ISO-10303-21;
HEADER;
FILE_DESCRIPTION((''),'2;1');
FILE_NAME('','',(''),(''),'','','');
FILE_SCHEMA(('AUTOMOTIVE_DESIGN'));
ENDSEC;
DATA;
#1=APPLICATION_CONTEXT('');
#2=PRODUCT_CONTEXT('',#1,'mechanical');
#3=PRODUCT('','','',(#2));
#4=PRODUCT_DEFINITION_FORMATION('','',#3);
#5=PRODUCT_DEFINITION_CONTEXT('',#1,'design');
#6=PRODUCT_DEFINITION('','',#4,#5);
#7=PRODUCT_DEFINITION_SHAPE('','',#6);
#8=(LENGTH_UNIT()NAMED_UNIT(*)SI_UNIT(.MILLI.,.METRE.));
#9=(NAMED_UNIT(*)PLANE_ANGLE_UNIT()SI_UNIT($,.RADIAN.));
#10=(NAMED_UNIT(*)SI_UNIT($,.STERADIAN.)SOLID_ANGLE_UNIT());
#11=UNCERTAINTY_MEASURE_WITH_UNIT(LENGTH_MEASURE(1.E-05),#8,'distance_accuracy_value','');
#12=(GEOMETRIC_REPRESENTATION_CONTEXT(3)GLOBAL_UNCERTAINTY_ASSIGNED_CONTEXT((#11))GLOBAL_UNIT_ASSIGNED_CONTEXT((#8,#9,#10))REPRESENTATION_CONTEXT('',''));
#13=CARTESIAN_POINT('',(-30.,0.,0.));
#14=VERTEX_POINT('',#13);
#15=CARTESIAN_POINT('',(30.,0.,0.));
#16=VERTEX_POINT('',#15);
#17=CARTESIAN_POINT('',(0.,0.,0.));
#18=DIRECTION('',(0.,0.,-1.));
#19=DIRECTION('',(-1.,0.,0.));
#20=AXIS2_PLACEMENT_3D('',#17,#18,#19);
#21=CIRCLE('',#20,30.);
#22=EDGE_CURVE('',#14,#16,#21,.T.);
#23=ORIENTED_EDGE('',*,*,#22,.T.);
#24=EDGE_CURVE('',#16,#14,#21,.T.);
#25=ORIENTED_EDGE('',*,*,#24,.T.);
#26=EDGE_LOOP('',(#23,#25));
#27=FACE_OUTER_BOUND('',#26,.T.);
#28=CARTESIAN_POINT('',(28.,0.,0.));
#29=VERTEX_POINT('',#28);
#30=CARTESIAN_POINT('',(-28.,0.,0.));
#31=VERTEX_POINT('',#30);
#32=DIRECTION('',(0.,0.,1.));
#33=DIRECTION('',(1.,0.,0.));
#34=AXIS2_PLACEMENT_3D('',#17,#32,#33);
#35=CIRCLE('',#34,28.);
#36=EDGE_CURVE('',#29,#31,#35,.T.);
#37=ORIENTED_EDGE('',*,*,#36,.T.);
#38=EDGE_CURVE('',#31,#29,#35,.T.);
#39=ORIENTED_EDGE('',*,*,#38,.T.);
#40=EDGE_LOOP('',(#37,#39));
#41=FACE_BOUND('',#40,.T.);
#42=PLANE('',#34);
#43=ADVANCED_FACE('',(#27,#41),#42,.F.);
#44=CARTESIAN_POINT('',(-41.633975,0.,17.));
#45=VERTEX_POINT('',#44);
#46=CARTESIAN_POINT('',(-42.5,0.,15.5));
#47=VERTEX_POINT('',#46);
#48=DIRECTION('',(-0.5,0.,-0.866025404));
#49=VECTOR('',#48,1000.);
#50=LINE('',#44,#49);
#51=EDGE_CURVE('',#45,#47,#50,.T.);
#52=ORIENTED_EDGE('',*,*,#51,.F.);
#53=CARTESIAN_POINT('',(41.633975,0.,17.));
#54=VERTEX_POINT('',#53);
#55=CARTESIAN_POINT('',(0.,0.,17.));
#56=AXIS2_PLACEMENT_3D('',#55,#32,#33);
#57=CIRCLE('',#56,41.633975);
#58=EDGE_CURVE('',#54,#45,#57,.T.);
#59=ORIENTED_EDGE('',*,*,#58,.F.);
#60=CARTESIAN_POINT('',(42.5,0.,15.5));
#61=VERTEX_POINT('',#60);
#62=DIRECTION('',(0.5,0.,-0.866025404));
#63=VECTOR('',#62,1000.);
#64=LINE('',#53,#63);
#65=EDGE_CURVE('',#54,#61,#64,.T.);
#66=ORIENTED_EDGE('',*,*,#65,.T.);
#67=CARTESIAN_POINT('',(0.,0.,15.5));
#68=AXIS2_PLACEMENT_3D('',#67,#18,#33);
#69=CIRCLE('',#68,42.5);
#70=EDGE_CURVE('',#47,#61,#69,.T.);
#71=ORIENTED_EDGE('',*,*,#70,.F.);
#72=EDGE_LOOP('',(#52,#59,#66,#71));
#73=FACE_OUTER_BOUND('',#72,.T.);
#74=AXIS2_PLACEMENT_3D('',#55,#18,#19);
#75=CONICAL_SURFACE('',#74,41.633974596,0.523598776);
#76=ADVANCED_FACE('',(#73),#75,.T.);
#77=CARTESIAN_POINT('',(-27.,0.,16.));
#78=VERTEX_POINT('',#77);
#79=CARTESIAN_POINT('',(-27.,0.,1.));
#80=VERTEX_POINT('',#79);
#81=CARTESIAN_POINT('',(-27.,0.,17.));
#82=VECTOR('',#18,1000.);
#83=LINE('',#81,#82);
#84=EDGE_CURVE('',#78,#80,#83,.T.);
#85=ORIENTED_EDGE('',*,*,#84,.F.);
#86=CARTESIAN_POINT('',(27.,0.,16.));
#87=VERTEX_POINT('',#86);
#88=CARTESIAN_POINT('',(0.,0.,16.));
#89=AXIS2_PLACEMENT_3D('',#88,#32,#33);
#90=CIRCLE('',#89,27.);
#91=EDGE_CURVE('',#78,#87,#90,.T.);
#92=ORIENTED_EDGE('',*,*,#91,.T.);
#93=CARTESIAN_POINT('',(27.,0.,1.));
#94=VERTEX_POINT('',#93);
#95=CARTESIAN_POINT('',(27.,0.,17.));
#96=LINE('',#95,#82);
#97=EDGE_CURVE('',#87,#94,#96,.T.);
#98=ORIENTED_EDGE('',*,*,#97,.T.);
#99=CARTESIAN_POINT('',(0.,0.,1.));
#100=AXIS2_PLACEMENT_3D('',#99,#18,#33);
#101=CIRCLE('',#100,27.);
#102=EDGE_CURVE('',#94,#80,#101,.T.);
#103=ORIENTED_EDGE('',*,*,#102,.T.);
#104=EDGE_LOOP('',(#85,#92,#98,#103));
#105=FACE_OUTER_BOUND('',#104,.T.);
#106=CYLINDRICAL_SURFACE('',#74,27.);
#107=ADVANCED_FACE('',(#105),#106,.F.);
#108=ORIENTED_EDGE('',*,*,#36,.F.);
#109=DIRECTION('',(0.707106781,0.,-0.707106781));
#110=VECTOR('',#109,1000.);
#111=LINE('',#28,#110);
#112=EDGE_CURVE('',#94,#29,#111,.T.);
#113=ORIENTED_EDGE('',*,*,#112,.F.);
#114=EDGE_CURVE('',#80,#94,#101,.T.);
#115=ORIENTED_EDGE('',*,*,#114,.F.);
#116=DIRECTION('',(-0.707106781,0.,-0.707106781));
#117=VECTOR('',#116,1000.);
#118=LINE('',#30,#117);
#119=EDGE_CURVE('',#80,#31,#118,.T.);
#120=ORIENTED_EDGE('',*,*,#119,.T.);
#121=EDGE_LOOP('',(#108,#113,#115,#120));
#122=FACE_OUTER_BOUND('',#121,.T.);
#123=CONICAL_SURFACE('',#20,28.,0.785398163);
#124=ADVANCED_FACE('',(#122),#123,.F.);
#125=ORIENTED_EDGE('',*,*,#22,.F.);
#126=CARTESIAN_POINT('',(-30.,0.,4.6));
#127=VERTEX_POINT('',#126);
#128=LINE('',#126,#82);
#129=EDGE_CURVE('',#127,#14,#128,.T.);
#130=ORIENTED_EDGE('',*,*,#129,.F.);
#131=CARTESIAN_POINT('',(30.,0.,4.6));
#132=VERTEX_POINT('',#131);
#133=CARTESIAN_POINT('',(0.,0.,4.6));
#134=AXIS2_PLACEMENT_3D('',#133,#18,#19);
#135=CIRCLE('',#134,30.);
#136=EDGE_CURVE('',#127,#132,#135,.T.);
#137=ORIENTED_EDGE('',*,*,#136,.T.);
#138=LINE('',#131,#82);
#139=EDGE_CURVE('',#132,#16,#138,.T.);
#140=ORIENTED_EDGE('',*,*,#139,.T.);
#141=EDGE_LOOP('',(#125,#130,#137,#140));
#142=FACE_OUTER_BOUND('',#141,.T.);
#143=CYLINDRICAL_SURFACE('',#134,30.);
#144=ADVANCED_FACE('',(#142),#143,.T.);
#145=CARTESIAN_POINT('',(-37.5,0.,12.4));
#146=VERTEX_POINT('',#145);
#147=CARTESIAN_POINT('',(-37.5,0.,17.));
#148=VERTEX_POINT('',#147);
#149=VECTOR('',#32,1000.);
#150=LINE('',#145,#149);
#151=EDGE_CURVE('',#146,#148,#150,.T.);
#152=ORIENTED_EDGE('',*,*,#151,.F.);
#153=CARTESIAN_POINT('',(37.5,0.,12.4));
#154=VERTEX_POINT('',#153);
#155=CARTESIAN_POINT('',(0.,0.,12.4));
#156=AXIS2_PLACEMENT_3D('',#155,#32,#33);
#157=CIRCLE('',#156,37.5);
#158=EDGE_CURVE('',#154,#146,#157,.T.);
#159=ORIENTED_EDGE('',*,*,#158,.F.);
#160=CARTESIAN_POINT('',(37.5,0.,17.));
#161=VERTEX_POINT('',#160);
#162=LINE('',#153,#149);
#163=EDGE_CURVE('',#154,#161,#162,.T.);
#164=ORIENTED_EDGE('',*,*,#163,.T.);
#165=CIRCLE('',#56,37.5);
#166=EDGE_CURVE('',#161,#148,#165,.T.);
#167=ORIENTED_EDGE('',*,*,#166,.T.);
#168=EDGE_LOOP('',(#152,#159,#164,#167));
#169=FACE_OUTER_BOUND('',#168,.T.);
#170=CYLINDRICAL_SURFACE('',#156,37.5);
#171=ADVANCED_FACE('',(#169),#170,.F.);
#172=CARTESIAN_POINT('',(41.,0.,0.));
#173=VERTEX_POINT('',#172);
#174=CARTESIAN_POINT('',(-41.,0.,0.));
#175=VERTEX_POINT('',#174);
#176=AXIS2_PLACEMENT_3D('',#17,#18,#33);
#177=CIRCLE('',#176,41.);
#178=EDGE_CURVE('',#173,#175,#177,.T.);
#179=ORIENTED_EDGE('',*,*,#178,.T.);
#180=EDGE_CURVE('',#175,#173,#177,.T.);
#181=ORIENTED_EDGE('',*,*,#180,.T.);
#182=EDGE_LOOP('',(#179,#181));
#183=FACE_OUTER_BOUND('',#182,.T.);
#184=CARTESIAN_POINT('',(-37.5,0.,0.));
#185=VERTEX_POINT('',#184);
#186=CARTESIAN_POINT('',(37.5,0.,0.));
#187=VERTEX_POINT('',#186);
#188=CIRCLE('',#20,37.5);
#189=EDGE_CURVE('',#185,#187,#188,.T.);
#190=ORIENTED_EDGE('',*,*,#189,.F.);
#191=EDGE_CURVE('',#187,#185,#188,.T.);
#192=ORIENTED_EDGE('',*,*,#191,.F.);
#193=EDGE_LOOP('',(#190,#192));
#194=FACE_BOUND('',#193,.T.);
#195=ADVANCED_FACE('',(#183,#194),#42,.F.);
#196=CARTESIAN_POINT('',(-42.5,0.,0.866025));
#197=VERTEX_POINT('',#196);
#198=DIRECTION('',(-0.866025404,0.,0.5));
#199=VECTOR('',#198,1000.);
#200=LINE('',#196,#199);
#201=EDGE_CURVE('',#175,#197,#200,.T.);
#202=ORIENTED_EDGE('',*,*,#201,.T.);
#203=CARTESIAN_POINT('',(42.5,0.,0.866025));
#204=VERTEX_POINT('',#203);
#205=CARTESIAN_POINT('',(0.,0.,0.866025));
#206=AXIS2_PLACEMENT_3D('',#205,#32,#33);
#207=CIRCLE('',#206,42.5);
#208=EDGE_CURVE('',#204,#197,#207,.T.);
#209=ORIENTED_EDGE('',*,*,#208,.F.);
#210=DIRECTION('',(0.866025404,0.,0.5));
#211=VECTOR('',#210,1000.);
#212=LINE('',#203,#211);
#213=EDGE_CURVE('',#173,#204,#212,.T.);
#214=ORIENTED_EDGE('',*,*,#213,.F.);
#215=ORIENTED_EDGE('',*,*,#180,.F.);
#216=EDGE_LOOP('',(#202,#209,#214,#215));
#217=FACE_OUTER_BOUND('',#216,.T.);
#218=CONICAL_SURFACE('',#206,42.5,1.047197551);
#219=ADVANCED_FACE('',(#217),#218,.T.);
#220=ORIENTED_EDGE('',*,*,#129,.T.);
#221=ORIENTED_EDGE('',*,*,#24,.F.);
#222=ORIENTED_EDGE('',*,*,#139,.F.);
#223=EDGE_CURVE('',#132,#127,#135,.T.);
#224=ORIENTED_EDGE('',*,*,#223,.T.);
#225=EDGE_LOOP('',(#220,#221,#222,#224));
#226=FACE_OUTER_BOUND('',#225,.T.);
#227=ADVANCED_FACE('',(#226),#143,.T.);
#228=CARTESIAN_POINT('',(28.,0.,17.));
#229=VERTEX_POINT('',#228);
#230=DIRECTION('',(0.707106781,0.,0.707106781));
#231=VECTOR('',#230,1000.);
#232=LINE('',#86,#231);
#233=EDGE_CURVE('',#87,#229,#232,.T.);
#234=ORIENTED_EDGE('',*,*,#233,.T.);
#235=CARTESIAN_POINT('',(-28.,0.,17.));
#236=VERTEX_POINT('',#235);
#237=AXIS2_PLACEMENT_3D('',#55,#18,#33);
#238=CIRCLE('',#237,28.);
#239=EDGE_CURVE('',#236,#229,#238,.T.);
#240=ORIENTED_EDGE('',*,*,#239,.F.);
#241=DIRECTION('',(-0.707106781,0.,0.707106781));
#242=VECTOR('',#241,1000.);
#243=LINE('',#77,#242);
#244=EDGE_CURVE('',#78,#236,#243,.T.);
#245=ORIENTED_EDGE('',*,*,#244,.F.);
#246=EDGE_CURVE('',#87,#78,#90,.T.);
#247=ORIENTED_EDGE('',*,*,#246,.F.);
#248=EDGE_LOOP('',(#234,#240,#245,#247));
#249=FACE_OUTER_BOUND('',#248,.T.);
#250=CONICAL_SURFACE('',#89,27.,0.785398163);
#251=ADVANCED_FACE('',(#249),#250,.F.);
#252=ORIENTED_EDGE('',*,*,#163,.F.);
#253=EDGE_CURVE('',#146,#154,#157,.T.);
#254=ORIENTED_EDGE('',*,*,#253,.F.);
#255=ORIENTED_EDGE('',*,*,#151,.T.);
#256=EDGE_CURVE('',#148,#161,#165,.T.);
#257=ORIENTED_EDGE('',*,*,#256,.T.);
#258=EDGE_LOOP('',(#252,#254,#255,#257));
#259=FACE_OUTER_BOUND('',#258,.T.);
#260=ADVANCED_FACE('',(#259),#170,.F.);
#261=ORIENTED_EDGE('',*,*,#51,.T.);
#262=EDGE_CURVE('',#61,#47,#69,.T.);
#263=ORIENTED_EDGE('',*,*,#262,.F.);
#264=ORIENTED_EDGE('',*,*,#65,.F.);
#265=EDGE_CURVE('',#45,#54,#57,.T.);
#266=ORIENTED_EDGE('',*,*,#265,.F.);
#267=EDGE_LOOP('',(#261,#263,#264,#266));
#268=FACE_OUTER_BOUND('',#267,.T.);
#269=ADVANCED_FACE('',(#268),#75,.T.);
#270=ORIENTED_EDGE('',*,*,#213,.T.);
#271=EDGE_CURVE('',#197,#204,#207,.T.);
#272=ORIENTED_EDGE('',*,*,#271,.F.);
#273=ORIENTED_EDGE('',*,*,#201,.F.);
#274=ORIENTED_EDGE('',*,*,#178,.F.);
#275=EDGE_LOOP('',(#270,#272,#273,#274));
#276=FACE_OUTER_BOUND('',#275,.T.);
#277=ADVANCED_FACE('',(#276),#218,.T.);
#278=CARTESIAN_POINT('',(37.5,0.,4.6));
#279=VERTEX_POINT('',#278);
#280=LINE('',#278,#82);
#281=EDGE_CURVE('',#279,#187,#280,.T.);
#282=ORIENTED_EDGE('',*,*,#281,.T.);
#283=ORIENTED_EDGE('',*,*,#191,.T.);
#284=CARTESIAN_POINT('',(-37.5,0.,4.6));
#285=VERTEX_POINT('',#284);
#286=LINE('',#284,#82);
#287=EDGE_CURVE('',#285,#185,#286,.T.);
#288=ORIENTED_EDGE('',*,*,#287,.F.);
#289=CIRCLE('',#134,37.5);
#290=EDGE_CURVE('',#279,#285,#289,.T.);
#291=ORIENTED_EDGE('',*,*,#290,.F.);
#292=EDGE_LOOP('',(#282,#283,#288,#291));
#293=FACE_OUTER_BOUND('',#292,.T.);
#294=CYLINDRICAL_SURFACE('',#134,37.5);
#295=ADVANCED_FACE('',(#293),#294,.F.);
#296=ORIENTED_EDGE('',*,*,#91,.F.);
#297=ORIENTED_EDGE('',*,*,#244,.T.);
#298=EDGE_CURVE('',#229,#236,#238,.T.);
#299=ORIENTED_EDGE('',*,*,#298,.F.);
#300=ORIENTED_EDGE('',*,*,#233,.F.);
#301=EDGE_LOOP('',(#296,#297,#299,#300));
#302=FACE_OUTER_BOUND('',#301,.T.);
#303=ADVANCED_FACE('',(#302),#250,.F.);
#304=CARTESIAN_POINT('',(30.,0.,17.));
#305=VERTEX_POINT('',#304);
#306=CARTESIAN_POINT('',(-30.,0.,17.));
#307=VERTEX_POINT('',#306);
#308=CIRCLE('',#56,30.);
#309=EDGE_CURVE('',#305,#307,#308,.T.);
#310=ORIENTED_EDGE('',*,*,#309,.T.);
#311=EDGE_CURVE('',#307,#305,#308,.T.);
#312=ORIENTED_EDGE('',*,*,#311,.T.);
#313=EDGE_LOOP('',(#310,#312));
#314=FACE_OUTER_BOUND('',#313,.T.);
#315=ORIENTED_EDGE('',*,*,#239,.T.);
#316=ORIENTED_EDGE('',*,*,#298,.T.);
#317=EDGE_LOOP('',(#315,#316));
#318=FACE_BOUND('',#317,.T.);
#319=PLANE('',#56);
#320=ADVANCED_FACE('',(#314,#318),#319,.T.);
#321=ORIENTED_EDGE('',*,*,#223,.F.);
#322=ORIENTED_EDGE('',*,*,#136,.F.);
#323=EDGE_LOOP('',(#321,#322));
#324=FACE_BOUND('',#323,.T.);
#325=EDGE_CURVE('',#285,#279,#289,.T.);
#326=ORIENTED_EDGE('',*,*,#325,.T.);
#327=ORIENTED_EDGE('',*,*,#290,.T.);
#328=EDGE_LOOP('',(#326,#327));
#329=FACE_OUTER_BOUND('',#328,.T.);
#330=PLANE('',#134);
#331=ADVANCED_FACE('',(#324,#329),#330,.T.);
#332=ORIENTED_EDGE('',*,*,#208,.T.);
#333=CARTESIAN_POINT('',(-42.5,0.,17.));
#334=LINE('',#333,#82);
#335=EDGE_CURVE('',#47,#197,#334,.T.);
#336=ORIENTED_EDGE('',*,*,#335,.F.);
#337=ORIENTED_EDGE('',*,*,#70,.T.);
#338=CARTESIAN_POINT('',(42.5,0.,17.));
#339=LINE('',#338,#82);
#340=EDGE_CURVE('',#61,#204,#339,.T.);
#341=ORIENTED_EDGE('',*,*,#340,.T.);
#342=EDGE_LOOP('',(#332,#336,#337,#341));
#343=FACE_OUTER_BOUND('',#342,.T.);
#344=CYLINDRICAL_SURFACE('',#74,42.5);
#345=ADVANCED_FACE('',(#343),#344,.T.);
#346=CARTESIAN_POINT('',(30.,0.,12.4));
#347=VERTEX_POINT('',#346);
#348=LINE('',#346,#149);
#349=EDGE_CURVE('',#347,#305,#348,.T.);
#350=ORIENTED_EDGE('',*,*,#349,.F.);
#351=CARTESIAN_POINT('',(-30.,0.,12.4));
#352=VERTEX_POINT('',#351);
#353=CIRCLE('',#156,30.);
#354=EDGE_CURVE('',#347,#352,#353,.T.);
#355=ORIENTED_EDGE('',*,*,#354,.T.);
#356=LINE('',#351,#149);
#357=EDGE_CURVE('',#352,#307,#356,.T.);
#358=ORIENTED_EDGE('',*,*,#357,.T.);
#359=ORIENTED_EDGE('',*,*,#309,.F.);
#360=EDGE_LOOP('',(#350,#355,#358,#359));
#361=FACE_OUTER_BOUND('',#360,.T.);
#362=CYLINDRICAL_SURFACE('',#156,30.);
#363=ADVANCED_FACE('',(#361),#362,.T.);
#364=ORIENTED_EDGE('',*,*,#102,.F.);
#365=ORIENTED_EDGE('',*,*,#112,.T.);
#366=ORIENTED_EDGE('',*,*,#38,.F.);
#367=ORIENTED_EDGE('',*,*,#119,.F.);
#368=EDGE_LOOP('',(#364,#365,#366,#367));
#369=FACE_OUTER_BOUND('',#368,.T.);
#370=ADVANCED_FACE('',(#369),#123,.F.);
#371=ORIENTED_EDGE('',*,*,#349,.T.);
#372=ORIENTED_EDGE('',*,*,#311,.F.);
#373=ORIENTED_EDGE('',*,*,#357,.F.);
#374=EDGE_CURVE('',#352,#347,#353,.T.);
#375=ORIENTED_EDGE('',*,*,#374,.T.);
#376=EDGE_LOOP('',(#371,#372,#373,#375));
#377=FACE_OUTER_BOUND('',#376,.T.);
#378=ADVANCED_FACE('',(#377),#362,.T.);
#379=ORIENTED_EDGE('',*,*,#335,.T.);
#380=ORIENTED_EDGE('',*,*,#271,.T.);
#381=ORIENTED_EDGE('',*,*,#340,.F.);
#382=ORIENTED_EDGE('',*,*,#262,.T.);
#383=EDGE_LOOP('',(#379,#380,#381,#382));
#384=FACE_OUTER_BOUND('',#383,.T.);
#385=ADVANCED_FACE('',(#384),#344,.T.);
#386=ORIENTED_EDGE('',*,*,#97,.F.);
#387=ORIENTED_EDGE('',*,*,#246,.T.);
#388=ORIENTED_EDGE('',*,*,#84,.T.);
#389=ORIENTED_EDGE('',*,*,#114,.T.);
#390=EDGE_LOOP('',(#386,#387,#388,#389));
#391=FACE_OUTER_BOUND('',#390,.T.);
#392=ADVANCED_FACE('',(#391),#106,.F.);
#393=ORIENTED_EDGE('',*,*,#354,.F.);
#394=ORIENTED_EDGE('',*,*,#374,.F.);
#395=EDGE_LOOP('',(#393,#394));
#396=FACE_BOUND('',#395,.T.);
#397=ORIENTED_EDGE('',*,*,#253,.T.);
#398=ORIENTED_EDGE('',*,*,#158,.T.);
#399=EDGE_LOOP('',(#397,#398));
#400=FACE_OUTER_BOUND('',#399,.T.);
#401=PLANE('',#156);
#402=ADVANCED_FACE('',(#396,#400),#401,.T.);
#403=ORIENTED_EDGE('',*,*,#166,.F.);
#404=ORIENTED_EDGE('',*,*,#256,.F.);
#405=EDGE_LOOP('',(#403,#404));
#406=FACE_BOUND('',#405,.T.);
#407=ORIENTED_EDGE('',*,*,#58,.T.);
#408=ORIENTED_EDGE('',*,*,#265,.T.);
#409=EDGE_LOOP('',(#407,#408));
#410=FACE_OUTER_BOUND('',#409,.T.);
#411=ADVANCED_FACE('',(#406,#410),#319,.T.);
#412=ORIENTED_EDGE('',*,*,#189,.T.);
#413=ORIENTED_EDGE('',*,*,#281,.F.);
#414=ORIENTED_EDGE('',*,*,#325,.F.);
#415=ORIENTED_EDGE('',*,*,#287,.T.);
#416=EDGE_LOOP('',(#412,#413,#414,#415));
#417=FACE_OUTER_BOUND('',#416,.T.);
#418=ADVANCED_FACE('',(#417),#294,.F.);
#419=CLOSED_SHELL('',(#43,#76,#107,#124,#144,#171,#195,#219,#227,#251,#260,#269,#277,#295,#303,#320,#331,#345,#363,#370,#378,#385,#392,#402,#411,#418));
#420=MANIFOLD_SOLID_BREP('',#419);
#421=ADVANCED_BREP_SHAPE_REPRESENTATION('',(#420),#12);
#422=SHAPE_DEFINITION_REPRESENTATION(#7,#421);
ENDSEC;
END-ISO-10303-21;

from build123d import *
from OCP.BRepFilletAPI import BRepFilletAPI_MakeChamfer

# Parameters (mm, degrees)
SKETCH1_R           = 42.5
SKETCH1_R_2         = 27
BOSS_EXTRUDE1_DEPTH = 17
SKETCH2_R           = 37.5
SKETCH2_R_2         = 30
CUT_EXTRUDE1_DEPTH  = 4.6
CUT_EXTRUDE2_START  = -4.6
SKETCH3_R           = 37.5
SKETCH3_R_2         = 30
CUT_EXTRUDE2_DEPTH  = 4.6
CHAMFER1_SIZE       = 1.5
CHAMFER1_SIZE2      = 0.866025404
CHAMFER2_SIZE       = 1


with BuildPart() as part:
    # Sketch1 → Boss-Extrude1 (new body)
    with BuildSketch(Plane.XY):
        Circle(SKETCH1_R)
        Circle(SKETCH1_R_2, mode=Mode.SUBTRACT)
    extrude(amount=BOSS_EXTRUDE1_DEPTH)

    # Sketch2 → Cut-Extrude1 (cut)
    with BuildSketch(Plane.XY.offset(17)):
        Circle(SKETCH2_R)
        Circle(SKETCH2_R_2, mode=Mode.SUBTRACT)
    extrude(amount=-CUT_EXTRUDE1_DEPTH, mode=Mode.SUBTRACT)

    # Sketch3 → Cut-Extrude2 (cut)
    with BuildSketch(Plane(origin=(0, 0, 0), x_dir=(-1, 0, 0), z_dir=(0, 0, -1)).offset(CUT_EXTRUDE2_START)):
        with Locations(Location((0, 0, 0), (0, 0, 180))):
            Circle(SKETCH3_R)
        with Locations(Location((0, 0, 0), (0, 0, 180))):
            Circle(SKETCH3_R_2, mode=Mode.SUBTRACT)
    extrude(amount=CUT_EXTRUDE2_DEPTH, mode=Mode.SUBTRACT)

    # Chamfer1: one chamfer whose edges measure the first distance from different faces: ONE call of the kernel's chamfer builder (chamfer() names one face for all edges)
    chamfer1_edges_1 = [part.edges().sort_by_distance(p)[0] for p in [
        (-42.5, 0, 0),
    ]]
    chamfer1_side_1 = [part.faces().sort_by_distance(p)[0] for p in [
        (-41.297918472, 0, 0),
    ]]
    chamfer1_edges_2 = [part.edges().sort_by_distance(p)[0] for p in [
        (-42.5, 0, 17),
    ]]
    chamfer1_side_2 = [part.faces().sort_by_distance(p)[0] for p in [
        (-42.5, 0, 8.5),
    ]]
    chamfer1 = BRepFilletAPI_MakeChamfer(part.part.solid().wrapped)
    for e in chamfer1_edges_1:
        chamfer1.Add(CHAMFER1_SIZE, CHAMFER1_SIZE2, e.wrapped, chamfer1_side_1[0].wrapped)  # the first distance lies on this face
    for e in chamfer1_edges_2:
        chamfer1.Add(CHAMFER1_SIZE, CHAMFER1_SIZE2, e.wrapped, chamfer1_side_2[0].wrapped)  # the first distance lies on this face
    add(Compound.cast(chamfer1.Shape()), mode=Mode.REPLACE)

    # Chamfer2
    chamfer2_edges = [part.edges().sort_by_distance(p)[0] for p in [
        (-27, 0, 0),
        (-27, 0, 17),
    ]]
    chamfer(chamfer2_edges, length=CHAMFER2_SIZE)


solid = part.part
